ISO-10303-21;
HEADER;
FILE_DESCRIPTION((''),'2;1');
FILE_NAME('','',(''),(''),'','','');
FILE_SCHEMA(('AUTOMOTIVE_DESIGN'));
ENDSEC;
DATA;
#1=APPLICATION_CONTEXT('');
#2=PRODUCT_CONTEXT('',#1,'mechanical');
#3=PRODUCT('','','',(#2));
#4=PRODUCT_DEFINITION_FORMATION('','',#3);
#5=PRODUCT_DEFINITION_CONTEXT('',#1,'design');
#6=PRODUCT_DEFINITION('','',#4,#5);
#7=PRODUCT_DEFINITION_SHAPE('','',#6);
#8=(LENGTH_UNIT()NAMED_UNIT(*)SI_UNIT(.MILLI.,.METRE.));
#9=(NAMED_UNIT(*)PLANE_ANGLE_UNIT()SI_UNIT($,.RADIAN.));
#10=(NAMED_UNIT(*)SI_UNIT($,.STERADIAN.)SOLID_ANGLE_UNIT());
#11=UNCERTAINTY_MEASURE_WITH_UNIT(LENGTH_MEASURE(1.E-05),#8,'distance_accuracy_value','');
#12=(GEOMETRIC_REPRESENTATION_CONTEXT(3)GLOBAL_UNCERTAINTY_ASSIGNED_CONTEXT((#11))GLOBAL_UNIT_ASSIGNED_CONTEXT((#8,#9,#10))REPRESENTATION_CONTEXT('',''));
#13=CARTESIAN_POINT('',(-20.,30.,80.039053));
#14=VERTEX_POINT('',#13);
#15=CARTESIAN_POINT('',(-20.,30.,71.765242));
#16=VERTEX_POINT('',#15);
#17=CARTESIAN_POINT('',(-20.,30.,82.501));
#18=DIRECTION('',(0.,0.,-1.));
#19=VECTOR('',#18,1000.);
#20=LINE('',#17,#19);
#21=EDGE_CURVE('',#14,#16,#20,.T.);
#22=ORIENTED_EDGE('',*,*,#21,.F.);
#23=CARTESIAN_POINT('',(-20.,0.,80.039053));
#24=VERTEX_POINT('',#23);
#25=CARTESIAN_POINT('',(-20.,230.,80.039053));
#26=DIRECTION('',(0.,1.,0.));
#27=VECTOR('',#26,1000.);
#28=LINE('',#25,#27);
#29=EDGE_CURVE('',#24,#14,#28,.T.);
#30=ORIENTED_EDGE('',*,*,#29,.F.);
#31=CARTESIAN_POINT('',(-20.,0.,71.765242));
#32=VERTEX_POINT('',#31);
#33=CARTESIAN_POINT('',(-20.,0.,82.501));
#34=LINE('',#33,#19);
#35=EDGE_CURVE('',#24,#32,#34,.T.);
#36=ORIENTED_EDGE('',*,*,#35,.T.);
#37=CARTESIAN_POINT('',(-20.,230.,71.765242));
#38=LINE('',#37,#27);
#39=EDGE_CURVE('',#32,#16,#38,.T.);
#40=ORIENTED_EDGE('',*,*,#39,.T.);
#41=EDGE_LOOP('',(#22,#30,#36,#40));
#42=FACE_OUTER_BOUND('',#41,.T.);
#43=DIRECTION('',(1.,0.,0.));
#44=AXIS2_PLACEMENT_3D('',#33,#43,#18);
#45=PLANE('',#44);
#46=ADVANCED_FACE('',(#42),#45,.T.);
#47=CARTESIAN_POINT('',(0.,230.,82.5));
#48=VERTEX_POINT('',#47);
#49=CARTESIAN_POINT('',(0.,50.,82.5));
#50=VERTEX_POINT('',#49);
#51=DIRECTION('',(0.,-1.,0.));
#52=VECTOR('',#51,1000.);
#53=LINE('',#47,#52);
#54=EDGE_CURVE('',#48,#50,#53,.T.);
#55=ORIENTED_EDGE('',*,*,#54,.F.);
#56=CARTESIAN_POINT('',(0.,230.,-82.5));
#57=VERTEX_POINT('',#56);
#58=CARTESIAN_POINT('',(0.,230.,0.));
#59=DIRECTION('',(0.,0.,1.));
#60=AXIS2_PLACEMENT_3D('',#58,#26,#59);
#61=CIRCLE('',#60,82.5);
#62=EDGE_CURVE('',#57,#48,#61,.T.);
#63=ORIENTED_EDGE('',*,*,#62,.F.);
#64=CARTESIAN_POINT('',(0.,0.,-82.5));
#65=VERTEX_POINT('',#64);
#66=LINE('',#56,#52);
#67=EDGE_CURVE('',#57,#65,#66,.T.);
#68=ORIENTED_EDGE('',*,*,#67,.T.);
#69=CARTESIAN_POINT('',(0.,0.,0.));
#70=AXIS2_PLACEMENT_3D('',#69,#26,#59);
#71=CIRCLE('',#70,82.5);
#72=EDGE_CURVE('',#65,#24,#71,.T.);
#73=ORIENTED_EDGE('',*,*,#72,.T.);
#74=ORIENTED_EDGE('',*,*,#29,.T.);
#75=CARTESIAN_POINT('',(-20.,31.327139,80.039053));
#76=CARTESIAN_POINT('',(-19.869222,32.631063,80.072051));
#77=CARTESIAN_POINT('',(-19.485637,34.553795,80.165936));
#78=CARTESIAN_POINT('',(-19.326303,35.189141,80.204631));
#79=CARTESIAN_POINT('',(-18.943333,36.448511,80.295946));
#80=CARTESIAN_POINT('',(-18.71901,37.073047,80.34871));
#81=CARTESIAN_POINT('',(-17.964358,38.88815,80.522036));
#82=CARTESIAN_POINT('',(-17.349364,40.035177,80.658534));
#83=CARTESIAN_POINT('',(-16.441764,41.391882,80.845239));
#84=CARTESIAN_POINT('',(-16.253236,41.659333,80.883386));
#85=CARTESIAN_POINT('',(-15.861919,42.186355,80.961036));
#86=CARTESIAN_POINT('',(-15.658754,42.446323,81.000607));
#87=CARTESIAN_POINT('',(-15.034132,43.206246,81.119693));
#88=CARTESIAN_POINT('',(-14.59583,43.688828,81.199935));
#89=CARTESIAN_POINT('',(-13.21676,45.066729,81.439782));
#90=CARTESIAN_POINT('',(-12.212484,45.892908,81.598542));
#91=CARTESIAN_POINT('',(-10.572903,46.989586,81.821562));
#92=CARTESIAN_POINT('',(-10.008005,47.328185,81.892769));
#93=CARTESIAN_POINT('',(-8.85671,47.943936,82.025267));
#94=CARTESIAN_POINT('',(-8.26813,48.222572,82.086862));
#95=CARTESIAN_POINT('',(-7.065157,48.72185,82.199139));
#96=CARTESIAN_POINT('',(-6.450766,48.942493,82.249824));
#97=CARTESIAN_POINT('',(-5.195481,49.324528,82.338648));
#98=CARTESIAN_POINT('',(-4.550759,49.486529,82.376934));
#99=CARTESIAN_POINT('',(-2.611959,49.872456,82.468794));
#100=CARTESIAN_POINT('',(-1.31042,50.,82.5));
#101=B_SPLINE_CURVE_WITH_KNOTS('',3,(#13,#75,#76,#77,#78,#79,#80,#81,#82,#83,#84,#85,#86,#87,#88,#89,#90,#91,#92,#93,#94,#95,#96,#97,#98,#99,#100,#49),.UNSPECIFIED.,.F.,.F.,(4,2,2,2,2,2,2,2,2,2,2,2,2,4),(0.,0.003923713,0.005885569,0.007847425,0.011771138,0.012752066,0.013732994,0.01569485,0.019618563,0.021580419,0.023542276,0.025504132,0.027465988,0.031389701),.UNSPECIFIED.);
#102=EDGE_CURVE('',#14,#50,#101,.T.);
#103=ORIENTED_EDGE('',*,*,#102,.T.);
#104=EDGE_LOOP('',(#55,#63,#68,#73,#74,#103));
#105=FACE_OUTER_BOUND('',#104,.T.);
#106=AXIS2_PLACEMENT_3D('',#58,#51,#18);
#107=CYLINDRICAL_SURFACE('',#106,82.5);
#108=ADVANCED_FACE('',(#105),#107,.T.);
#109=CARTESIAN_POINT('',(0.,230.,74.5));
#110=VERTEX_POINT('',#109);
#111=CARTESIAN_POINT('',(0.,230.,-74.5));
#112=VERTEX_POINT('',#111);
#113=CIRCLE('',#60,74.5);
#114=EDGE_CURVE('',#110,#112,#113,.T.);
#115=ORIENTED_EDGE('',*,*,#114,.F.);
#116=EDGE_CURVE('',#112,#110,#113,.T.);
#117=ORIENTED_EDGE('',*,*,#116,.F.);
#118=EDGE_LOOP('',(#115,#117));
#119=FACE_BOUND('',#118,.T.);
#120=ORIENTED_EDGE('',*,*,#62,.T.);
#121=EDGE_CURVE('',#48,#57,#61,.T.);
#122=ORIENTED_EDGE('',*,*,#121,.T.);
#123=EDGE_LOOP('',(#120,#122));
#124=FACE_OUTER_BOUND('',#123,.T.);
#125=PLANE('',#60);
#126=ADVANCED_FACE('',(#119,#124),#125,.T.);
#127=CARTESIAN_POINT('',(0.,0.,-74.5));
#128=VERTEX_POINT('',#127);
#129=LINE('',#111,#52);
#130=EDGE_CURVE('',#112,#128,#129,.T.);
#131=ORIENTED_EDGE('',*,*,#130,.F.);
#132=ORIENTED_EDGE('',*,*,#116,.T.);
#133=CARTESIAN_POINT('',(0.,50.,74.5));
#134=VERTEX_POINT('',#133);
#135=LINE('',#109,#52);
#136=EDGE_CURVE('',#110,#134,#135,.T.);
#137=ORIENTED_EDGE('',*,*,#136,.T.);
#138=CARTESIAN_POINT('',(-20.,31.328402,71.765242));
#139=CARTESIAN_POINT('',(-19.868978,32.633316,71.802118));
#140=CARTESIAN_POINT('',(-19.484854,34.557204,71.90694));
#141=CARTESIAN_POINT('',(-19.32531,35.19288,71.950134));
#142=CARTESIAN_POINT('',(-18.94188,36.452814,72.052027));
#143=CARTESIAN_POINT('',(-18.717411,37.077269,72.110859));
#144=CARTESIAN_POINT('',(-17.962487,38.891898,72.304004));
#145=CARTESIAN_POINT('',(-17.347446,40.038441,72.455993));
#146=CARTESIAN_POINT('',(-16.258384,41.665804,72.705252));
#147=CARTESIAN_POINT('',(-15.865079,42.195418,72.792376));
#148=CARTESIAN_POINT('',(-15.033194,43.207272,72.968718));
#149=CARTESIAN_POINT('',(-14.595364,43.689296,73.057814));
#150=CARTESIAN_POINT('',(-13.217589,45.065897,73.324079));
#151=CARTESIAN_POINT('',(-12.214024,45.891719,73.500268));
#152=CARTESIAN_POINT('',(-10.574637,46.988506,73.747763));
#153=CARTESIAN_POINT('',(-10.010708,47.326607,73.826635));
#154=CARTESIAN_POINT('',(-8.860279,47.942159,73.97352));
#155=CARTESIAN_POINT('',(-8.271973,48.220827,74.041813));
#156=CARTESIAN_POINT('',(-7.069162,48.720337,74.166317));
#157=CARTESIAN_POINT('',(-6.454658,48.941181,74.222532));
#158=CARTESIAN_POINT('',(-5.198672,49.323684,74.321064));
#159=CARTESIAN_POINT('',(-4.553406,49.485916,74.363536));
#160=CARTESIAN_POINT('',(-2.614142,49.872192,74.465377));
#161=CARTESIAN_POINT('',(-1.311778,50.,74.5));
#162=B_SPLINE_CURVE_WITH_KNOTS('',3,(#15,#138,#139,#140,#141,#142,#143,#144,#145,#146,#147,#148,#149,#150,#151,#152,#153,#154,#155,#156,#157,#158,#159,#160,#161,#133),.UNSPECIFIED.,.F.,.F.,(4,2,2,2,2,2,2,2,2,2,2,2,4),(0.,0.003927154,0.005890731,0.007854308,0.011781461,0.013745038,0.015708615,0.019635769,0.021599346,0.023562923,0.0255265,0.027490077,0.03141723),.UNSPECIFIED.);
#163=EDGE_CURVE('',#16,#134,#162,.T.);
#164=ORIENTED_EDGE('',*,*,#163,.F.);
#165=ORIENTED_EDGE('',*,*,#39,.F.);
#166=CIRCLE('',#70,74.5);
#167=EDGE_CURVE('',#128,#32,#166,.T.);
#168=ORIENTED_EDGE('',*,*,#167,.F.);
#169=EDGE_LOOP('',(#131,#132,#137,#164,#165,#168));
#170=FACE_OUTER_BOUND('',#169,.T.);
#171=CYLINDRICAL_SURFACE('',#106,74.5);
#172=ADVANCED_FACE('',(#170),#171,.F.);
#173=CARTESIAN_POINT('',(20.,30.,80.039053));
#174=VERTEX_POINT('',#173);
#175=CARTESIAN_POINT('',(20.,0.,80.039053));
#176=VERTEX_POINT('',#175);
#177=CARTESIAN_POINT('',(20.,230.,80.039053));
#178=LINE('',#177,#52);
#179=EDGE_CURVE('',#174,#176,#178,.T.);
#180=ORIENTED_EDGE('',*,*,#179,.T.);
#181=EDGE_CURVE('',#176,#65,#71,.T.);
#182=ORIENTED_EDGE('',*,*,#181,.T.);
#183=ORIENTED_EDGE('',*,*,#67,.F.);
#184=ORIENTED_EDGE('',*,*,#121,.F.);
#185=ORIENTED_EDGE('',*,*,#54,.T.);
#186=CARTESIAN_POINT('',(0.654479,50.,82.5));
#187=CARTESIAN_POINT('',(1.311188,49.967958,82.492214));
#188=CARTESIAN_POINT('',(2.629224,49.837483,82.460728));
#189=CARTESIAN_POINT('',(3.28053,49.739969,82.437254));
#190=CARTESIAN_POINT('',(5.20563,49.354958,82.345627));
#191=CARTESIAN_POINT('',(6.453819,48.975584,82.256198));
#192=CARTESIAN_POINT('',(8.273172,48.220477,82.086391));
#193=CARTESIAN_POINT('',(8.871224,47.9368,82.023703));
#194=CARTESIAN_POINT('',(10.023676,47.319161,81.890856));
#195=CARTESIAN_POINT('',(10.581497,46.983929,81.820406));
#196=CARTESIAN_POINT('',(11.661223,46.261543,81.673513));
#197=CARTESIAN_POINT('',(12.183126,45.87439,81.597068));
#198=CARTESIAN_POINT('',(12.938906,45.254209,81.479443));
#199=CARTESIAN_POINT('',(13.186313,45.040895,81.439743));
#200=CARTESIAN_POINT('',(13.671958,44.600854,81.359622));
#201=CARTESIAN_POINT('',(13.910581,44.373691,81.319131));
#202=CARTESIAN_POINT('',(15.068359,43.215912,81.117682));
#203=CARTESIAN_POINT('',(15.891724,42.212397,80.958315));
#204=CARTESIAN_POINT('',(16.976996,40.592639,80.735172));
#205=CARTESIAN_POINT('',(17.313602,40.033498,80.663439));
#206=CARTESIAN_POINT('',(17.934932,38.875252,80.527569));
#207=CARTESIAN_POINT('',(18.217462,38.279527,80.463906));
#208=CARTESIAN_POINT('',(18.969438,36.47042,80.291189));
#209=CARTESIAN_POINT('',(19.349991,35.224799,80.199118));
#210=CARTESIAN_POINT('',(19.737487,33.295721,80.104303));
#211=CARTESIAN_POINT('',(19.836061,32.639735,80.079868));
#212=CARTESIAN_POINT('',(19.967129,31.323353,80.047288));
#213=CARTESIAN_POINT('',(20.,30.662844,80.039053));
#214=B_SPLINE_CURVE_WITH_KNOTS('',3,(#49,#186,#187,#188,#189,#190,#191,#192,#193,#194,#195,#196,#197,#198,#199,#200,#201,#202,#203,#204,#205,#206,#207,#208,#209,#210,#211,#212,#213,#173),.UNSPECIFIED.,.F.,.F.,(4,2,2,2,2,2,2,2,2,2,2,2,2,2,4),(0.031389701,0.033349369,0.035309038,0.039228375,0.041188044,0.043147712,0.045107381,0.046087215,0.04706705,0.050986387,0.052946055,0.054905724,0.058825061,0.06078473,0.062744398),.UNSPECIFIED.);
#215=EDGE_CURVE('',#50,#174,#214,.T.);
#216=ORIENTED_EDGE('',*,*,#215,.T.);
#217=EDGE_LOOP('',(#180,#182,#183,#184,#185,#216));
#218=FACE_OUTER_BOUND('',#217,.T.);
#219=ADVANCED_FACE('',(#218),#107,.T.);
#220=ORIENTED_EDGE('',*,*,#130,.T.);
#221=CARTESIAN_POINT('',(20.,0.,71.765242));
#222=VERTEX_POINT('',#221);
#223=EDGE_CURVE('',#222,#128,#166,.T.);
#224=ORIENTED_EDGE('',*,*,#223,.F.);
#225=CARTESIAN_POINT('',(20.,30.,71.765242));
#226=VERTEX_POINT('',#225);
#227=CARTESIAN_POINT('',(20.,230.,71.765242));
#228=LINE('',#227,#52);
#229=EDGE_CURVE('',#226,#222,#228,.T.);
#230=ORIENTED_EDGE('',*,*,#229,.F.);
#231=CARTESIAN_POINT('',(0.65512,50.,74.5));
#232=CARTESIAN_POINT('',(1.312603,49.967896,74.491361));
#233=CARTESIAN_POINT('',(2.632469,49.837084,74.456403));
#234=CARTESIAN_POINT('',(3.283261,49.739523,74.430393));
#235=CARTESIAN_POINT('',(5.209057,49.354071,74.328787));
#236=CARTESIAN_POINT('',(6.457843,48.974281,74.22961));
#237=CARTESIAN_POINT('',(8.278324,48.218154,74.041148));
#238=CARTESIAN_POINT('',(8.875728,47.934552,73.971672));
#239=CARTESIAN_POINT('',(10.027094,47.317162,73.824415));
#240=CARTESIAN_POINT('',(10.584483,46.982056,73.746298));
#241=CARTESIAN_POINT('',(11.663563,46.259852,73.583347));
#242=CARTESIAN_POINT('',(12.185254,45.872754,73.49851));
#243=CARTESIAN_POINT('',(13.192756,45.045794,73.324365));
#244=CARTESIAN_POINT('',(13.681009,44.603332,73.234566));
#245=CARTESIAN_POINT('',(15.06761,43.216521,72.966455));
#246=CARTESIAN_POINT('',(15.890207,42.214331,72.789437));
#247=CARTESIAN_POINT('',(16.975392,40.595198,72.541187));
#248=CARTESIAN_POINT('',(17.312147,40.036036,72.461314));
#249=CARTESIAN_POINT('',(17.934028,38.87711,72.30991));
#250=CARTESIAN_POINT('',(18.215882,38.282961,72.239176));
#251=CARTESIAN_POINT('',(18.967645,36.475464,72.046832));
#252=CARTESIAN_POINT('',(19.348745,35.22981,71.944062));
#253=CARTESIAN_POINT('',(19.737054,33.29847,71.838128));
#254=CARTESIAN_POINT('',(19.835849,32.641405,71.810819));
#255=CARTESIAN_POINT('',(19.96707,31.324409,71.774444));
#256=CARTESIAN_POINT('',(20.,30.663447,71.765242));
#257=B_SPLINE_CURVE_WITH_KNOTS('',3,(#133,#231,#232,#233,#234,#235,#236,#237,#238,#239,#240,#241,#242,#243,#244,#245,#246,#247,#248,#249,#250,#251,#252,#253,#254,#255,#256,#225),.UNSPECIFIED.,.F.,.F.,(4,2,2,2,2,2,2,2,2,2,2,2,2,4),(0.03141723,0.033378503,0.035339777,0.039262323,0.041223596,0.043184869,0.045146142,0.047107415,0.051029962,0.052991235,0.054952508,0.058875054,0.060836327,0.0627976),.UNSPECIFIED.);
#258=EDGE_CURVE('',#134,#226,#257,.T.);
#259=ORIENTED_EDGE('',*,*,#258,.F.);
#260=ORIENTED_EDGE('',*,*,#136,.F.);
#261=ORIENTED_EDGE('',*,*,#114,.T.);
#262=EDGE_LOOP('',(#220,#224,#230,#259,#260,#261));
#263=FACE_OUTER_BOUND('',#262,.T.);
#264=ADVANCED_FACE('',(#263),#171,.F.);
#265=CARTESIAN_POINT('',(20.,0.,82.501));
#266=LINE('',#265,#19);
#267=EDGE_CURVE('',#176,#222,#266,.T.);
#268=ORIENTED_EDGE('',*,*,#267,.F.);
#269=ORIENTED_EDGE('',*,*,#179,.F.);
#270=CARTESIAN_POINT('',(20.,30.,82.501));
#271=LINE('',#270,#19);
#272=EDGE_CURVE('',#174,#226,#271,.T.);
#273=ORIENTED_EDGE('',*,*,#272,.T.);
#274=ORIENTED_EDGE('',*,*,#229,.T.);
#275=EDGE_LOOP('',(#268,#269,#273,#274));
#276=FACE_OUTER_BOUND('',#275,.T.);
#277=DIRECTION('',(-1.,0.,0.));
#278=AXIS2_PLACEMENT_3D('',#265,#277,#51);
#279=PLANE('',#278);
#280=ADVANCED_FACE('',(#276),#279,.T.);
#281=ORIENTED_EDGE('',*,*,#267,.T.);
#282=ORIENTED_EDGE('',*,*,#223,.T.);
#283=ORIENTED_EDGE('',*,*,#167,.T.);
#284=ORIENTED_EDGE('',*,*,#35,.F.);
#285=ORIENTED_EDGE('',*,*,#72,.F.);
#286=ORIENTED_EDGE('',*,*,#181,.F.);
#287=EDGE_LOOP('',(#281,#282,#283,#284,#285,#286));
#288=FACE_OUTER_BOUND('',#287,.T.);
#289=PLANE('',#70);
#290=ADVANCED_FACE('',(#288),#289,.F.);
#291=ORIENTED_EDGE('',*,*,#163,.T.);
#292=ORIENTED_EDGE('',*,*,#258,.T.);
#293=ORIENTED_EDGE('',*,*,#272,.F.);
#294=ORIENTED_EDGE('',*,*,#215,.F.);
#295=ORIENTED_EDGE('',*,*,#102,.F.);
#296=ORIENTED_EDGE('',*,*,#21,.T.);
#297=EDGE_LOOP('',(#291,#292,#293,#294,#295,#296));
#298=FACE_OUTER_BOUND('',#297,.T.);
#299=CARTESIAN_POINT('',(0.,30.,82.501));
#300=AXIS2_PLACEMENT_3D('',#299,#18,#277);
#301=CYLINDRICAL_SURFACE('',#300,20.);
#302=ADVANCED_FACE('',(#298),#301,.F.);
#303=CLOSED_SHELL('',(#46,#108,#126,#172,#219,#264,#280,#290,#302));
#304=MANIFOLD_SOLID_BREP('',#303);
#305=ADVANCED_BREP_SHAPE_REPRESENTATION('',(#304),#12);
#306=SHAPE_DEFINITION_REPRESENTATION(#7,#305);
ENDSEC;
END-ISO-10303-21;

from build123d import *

# Parameters (mm, degrees)
SKETCH1_R               = 82.5
SKETCH1_R_2             = 74.5
BOSS_EXTRUDE1_DEPTH     = 230
CUT_EXTRUDE1_REACH      = 259.9
CUT_EXTRUDE1_END_RADIUS = 82.5


with BuildPart() as part:
    # Sketch1 → Boss-Extrude1 (new body)
    with BuildSketch(Plane(origin=(0, 0, 0), x_dir=(1, 0, 0), z_dir=(0, 1, 0))):
        with Locations(Location((0, 0, 0), (0, 0, 270))):
            Circle(SKETCH1_R)
        with Locations(Location((0, 0, 0), (0, 0, 270))):
            Circle(SKETCH1_R_2, mode=Mode.SUBTRACT)
    extrude(amount=BOSS_EXTRUDE1_DEPTH)

    # Cut-Extrude1: up to this cylinder (the profile starts inside it)
    cut_extrude1_end = Plane(origin=(0, 15, 0), z_dir=(0, -1, 0)) * Cylinder(CUT_EXTRUDE1_END_RADIUS, 685.8, mode=Mode.PRIVATE)
    # Sketch2 → Cut-Extrude1 (cut, up to the surface)
    with BuildSketch(Plane.XY, mode=Mode.PRIVATE) as cut_extrude1_sk1:
        with BuildLine():
            Line((-20, 0), (-20, 30))
            ThreePointArc((-20, 30), (0, 50), (20, 30))
            Line((20, 30), (20, 0))
            ThreePointArc((20, 0), (0, -20), (-20, 0))
        make_face()
    cut_extrude1_tool1 = extrude(cut_extrude1_sk1.sketch, amount=CUT_EXTRUDE1_REACH, mode=Mode.PRIVATE) & cut_extrude1_end
    add(cut_extrude1_tool1.solids().sort_by_distance((0, 15, 0))[0], mode=Mode.SUBTRACT)


solid = part.part
